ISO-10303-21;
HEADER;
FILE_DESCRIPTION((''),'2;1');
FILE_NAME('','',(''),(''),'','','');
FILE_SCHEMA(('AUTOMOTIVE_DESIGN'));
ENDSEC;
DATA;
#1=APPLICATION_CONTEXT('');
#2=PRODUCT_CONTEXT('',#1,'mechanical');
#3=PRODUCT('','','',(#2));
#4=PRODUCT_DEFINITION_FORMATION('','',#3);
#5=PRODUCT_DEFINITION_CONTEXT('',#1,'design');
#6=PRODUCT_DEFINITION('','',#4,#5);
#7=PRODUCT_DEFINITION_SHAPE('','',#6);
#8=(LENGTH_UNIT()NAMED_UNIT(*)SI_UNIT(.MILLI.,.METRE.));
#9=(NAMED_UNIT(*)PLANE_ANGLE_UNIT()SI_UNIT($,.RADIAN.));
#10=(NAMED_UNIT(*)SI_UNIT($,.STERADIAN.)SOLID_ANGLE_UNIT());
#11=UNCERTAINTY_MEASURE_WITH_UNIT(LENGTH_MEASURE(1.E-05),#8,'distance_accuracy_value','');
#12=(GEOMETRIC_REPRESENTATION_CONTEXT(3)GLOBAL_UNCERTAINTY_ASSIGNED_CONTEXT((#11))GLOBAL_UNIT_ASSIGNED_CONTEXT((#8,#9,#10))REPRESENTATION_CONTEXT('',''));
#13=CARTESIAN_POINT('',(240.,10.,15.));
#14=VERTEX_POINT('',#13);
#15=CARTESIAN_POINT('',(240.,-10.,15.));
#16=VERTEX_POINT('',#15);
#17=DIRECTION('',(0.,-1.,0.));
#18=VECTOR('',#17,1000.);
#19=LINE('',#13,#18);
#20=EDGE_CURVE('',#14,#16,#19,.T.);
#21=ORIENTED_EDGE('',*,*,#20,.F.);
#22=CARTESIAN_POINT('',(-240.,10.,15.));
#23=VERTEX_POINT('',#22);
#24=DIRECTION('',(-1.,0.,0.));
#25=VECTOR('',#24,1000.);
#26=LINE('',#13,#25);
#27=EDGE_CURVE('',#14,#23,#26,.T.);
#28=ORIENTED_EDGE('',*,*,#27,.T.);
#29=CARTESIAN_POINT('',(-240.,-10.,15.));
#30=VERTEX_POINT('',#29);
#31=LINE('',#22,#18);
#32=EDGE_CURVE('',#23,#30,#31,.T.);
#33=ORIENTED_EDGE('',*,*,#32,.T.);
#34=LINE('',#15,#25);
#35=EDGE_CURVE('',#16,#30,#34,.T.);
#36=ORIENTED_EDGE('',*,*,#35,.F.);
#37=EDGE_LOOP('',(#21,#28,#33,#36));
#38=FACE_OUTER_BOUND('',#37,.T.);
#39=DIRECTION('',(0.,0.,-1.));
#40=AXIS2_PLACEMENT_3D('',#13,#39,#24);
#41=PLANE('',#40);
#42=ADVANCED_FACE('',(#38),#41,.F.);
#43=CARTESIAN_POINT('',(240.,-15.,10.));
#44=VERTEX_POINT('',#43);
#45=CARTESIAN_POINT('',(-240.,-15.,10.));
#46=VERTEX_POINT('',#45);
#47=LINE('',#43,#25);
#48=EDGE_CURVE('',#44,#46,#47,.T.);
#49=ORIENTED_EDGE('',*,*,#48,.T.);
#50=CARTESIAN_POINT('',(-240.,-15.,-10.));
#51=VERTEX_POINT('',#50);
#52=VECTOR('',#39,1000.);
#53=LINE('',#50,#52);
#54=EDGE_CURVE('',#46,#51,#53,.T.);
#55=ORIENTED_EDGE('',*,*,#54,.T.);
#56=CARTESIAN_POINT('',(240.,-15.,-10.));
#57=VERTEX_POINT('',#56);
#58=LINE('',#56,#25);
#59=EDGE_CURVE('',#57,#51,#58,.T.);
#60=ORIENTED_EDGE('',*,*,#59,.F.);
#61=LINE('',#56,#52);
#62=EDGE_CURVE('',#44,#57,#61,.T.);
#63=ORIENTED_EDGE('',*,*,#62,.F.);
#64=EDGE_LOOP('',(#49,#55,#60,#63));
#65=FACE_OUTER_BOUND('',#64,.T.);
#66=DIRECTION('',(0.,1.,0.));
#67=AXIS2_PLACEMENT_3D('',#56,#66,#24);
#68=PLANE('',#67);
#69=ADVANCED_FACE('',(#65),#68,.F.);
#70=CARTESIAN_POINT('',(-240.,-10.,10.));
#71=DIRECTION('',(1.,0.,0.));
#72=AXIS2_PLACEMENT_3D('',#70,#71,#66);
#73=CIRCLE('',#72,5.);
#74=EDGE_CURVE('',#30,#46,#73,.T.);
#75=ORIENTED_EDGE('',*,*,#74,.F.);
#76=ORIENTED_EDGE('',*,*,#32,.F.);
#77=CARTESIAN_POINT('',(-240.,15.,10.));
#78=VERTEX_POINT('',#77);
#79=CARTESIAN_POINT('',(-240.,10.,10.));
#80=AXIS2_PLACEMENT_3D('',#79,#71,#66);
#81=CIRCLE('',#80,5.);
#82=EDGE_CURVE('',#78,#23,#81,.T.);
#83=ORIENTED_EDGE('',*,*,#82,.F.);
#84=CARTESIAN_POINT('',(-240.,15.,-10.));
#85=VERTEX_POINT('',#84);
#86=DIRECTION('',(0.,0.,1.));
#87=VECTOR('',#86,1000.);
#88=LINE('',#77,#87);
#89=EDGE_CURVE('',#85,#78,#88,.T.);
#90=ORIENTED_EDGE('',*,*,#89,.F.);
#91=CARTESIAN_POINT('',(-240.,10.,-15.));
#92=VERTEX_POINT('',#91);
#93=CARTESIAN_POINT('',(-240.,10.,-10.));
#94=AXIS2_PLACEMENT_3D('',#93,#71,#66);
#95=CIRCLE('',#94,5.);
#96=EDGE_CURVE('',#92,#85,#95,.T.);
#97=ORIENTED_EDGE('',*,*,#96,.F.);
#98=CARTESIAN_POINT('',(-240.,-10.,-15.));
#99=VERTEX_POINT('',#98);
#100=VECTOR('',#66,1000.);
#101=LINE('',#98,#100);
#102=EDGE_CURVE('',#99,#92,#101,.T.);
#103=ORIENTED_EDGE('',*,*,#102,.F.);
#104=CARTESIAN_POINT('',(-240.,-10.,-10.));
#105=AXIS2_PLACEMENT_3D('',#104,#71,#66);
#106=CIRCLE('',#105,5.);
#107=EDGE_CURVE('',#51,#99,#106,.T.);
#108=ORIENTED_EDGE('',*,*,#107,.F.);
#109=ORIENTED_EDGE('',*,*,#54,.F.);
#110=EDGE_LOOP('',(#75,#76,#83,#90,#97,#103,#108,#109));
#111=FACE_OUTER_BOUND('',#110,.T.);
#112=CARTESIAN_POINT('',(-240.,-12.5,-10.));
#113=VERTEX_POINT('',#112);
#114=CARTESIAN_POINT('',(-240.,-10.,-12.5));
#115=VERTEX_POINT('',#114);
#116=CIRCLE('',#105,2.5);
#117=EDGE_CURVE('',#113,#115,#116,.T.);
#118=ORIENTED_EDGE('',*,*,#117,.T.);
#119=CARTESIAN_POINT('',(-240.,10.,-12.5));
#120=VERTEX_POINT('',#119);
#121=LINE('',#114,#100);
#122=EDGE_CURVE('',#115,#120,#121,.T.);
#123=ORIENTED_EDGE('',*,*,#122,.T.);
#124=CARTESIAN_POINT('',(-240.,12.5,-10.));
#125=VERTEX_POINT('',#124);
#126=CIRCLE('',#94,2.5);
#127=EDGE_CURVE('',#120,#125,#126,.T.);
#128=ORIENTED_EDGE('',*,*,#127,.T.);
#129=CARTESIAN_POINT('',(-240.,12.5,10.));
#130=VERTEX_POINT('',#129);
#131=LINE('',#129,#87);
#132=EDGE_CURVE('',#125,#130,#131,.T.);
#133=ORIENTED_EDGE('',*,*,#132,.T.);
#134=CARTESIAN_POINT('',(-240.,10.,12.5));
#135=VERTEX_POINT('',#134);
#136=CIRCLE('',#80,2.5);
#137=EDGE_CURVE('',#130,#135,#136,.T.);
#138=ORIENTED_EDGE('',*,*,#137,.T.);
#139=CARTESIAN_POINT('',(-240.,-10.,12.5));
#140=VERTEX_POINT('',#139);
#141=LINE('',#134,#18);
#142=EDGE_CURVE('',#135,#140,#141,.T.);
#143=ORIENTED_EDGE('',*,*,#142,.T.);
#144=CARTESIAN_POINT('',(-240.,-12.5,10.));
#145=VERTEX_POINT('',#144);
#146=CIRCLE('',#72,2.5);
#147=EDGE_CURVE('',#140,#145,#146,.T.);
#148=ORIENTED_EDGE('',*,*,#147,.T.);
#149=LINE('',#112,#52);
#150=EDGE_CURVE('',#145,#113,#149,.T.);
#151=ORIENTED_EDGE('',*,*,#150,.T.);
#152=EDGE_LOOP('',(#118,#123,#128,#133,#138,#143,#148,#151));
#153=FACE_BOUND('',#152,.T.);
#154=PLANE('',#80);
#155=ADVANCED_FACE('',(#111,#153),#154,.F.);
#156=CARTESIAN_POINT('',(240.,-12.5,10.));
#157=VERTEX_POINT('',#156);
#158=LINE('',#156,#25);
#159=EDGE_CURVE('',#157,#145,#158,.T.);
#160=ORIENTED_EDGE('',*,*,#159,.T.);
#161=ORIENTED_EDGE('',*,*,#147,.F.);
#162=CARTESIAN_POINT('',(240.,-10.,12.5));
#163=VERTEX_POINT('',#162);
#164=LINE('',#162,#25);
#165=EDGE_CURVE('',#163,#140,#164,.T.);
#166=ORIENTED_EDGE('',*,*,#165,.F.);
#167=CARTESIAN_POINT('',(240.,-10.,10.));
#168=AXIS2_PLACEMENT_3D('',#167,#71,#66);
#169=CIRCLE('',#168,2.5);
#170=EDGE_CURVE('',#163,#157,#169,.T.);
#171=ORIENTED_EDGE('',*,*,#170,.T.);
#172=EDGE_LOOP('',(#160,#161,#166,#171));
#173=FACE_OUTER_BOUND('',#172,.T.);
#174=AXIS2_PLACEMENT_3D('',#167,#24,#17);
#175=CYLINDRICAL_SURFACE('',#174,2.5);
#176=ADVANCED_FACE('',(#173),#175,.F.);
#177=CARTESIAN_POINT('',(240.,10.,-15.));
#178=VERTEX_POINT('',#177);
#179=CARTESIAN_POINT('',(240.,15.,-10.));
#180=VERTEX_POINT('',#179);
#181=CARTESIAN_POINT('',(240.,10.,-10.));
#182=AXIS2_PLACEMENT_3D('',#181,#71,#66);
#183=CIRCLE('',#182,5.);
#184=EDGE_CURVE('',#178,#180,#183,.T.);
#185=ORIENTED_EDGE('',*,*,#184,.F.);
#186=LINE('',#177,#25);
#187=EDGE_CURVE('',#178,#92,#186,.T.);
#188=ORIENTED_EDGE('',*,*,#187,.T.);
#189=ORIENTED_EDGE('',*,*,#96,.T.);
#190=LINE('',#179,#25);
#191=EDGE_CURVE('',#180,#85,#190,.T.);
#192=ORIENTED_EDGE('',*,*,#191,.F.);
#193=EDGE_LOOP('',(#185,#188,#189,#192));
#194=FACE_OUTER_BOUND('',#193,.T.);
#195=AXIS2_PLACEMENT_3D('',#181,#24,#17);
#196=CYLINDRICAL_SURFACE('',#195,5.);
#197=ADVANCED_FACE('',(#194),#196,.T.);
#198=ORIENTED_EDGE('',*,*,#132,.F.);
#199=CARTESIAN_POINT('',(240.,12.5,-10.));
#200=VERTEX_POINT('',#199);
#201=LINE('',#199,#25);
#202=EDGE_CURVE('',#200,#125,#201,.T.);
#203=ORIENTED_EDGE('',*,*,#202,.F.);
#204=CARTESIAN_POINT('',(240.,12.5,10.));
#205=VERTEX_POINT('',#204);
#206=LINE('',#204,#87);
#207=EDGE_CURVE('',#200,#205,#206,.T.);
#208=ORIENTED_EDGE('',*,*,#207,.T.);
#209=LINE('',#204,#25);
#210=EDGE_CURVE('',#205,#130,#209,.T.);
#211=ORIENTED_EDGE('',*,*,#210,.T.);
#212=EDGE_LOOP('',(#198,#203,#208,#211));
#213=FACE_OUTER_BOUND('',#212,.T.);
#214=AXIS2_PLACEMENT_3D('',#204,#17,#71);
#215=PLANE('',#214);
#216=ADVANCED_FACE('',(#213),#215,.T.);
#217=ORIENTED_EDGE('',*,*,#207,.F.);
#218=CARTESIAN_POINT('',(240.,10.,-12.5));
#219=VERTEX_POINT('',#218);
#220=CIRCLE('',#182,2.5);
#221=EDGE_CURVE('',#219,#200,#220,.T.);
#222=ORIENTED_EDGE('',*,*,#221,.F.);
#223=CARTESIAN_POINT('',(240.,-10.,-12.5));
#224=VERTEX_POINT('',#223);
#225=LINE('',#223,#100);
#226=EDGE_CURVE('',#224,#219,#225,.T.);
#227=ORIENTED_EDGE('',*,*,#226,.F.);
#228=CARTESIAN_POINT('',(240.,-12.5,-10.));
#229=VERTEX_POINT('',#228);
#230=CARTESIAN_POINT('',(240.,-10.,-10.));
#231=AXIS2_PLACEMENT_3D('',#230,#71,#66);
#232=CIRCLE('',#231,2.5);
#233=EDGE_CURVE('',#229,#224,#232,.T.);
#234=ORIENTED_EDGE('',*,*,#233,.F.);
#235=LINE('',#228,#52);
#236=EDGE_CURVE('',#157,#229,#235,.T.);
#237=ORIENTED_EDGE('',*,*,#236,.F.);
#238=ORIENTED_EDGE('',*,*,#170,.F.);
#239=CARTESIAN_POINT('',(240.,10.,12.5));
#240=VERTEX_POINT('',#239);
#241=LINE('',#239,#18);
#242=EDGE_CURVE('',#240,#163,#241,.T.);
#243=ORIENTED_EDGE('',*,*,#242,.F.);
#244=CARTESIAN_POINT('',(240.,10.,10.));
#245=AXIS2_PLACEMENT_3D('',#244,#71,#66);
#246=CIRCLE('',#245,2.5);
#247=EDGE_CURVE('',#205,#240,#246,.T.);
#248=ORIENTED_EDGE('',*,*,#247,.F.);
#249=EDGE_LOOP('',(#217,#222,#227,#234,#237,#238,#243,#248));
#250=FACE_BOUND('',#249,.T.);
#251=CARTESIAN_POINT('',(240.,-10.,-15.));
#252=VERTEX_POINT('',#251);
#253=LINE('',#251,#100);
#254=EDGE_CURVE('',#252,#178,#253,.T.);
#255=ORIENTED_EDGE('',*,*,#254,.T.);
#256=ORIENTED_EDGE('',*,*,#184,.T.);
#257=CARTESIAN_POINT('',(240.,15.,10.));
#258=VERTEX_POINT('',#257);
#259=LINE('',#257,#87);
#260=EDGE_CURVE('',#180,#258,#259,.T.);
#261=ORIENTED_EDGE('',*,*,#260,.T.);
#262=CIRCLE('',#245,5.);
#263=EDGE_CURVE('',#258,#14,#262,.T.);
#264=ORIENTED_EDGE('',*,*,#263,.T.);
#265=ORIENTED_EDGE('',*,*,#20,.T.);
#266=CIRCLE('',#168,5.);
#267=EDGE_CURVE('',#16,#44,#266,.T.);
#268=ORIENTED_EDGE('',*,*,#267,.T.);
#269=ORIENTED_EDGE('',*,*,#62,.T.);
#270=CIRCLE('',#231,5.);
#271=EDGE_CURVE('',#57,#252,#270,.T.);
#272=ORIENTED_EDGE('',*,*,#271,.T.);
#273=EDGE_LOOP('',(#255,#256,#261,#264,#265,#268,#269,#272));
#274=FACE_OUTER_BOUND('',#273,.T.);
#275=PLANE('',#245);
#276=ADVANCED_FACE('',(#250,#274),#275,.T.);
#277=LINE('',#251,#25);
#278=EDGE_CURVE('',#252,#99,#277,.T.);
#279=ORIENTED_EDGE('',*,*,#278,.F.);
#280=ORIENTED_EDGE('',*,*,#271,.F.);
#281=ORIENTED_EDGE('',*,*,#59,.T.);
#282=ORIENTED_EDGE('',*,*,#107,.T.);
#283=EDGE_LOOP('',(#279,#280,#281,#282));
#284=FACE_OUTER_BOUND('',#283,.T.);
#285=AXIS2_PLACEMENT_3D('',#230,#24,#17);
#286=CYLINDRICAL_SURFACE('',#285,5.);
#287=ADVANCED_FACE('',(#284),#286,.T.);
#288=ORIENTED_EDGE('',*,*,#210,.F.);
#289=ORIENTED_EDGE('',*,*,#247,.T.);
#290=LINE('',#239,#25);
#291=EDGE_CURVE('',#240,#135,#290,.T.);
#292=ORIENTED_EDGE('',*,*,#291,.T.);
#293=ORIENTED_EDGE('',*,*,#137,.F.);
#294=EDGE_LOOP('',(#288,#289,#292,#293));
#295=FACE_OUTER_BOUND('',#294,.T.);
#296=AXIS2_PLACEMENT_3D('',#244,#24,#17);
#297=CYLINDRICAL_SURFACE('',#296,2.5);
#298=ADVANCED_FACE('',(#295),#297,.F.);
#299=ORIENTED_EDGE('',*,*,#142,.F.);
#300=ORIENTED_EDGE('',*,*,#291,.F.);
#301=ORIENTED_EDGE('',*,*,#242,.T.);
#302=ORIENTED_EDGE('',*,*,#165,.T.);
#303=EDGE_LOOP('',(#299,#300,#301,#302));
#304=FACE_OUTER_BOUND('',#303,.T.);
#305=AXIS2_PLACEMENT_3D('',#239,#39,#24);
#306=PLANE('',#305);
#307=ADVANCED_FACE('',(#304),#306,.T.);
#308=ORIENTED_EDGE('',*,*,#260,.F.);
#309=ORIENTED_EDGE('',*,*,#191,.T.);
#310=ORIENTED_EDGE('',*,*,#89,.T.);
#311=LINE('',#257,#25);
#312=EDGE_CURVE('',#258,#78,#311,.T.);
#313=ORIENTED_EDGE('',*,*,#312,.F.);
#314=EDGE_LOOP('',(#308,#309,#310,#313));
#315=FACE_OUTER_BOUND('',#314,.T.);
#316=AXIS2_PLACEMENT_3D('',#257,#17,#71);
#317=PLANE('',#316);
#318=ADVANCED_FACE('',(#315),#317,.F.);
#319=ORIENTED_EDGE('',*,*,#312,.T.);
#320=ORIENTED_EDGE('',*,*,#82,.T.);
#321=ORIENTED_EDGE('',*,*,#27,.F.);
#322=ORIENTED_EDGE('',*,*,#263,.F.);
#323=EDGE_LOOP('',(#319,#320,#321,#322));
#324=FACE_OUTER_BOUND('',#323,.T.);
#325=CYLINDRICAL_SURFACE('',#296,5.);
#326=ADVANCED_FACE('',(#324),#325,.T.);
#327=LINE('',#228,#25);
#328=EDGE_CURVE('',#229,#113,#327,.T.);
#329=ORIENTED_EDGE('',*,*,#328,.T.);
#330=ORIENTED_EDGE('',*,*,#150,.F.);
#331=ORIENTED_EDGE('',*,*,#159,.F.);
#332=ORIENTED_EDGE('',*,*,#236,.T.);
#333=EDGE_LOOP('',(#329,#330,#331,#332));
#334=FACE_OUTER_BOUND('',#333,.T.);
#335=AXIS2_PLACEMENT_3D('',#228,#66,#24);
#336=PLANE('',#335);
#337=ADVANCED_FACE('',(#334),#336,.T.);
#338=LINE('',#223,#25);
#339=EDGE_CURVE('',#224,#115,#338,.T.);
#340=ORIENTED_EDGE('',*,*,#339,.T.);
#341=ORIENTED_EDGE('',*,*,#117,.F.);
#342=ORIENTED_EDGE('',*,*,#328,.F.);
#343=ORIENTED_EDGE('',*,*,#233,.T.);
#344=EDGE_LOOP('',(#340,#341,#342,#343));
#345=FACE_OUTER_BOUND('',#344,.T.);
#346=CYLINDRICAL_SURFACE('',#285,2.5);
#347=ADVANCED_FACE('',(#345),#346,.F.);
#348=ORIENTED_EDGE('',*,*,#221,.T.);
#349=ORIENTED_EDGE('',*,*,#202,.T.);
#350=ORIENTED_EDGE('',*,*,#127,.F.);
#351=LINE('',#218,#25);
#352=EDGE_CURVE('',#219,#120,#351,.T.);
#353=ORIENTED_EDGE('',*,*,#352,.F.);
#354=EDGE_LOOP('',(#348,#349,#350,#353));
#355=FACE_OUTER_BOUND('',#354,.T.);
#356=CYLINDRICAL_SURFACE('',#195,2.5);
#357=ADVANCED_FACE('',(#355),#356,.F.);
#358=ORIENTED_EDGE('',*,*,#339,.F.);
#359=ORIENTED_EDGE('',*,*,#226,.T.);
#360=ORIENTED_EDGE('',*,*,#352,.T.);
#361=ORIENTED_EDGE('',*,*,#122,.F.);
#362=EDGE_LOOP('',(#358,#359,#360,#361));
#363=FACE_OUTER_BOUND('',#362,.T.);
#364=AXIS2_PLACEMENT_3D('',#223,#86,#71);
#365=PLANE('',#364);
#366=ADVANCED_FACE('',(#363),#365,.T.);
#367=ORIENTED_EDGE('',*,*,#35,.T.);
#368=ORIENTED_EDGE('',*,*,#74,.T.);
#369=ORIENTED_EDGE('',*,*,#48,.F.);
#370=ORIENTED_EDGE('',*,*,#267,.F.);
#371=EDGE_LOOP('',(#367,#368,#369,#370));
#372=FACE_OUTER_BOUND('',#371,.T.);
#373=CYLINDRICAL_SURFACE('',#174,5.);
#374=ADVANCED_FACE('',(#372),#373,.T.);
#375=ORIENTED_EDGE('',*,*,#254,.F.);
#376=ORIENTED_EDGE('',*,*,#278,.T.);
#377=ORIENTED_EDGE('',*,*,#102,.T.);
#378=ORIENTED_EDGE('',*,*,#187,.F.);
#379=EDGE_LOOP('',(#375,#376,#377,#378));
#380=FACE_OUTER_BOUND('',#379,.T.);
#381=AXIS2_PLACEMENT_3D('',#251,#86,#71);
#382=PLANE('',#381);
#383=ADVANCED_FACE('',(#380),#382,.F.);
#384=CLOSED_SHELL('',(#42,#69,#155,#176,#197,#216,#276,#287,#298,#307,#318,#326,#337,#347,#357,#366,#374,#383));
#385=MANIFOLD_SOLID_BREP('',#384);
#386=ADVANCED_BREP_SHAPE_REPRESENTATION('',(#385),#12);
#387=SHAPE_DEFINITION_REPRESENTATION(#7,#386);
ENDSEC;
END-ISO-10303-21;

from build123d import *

# Parameters (mm, degrees)
SQUARE_TUBE_30_X_30_X_2_5_DEPTH = 480


with BuildPart() as part:
    # Sketch16 → Square tube 30 X 30 X 2.5 (new body)
    with BuildSketch(Plane.YZ.offset(-240)):
        with BuildLine():
            Line((-10, -15), (10, -15))
            ThreePointArc((10, -15), (13.535533906, -13.535533906), (15, -10))
            Line((15, -10), (15, 10))
            ThreePointArc((15, 10), (13.535533906, 13.535533906), (10, 15))
            Line((10, 15), (-10, 15))
            ThreePointArc((-10, 15), (-13.535533906, 13.535533906), (-15, 10))
            Line((-15, 10), (-15, -10))
            ThreePointArc((-15, -10), (-13.535533906, -13.535533906), (-10, -15))
        make_face()
        with BuildLine():
            Line((-10, -12.5), (10, -12.5))
            ThreePointArc((10, -12.5), (11.767766953, -11.767766953), (12.5, -10))
            Line((12.5, -10), (12.5, 10))
            ThreePointArc((12.5, 10), (11.767766953, 11.767766953), (10, 12.5))
            Line((10, 12.5), (-10, 12.5))
            ThreePointArc((-10, 12.5), (-11.767766953, 11.767766953), (-12.5, 10))
            Line((-12.5, 10), (-12.5, -10))
            ThreePointArc((-12.5, -10), (-11.767766953, -11.767766953), (-10, -12.5))
        make_face(mode=Mode.SUBTRACT)
    extrude(amount=SQUARE_TUBE_30_X_30_X_2_5_DEPTH)


solid = part.part
